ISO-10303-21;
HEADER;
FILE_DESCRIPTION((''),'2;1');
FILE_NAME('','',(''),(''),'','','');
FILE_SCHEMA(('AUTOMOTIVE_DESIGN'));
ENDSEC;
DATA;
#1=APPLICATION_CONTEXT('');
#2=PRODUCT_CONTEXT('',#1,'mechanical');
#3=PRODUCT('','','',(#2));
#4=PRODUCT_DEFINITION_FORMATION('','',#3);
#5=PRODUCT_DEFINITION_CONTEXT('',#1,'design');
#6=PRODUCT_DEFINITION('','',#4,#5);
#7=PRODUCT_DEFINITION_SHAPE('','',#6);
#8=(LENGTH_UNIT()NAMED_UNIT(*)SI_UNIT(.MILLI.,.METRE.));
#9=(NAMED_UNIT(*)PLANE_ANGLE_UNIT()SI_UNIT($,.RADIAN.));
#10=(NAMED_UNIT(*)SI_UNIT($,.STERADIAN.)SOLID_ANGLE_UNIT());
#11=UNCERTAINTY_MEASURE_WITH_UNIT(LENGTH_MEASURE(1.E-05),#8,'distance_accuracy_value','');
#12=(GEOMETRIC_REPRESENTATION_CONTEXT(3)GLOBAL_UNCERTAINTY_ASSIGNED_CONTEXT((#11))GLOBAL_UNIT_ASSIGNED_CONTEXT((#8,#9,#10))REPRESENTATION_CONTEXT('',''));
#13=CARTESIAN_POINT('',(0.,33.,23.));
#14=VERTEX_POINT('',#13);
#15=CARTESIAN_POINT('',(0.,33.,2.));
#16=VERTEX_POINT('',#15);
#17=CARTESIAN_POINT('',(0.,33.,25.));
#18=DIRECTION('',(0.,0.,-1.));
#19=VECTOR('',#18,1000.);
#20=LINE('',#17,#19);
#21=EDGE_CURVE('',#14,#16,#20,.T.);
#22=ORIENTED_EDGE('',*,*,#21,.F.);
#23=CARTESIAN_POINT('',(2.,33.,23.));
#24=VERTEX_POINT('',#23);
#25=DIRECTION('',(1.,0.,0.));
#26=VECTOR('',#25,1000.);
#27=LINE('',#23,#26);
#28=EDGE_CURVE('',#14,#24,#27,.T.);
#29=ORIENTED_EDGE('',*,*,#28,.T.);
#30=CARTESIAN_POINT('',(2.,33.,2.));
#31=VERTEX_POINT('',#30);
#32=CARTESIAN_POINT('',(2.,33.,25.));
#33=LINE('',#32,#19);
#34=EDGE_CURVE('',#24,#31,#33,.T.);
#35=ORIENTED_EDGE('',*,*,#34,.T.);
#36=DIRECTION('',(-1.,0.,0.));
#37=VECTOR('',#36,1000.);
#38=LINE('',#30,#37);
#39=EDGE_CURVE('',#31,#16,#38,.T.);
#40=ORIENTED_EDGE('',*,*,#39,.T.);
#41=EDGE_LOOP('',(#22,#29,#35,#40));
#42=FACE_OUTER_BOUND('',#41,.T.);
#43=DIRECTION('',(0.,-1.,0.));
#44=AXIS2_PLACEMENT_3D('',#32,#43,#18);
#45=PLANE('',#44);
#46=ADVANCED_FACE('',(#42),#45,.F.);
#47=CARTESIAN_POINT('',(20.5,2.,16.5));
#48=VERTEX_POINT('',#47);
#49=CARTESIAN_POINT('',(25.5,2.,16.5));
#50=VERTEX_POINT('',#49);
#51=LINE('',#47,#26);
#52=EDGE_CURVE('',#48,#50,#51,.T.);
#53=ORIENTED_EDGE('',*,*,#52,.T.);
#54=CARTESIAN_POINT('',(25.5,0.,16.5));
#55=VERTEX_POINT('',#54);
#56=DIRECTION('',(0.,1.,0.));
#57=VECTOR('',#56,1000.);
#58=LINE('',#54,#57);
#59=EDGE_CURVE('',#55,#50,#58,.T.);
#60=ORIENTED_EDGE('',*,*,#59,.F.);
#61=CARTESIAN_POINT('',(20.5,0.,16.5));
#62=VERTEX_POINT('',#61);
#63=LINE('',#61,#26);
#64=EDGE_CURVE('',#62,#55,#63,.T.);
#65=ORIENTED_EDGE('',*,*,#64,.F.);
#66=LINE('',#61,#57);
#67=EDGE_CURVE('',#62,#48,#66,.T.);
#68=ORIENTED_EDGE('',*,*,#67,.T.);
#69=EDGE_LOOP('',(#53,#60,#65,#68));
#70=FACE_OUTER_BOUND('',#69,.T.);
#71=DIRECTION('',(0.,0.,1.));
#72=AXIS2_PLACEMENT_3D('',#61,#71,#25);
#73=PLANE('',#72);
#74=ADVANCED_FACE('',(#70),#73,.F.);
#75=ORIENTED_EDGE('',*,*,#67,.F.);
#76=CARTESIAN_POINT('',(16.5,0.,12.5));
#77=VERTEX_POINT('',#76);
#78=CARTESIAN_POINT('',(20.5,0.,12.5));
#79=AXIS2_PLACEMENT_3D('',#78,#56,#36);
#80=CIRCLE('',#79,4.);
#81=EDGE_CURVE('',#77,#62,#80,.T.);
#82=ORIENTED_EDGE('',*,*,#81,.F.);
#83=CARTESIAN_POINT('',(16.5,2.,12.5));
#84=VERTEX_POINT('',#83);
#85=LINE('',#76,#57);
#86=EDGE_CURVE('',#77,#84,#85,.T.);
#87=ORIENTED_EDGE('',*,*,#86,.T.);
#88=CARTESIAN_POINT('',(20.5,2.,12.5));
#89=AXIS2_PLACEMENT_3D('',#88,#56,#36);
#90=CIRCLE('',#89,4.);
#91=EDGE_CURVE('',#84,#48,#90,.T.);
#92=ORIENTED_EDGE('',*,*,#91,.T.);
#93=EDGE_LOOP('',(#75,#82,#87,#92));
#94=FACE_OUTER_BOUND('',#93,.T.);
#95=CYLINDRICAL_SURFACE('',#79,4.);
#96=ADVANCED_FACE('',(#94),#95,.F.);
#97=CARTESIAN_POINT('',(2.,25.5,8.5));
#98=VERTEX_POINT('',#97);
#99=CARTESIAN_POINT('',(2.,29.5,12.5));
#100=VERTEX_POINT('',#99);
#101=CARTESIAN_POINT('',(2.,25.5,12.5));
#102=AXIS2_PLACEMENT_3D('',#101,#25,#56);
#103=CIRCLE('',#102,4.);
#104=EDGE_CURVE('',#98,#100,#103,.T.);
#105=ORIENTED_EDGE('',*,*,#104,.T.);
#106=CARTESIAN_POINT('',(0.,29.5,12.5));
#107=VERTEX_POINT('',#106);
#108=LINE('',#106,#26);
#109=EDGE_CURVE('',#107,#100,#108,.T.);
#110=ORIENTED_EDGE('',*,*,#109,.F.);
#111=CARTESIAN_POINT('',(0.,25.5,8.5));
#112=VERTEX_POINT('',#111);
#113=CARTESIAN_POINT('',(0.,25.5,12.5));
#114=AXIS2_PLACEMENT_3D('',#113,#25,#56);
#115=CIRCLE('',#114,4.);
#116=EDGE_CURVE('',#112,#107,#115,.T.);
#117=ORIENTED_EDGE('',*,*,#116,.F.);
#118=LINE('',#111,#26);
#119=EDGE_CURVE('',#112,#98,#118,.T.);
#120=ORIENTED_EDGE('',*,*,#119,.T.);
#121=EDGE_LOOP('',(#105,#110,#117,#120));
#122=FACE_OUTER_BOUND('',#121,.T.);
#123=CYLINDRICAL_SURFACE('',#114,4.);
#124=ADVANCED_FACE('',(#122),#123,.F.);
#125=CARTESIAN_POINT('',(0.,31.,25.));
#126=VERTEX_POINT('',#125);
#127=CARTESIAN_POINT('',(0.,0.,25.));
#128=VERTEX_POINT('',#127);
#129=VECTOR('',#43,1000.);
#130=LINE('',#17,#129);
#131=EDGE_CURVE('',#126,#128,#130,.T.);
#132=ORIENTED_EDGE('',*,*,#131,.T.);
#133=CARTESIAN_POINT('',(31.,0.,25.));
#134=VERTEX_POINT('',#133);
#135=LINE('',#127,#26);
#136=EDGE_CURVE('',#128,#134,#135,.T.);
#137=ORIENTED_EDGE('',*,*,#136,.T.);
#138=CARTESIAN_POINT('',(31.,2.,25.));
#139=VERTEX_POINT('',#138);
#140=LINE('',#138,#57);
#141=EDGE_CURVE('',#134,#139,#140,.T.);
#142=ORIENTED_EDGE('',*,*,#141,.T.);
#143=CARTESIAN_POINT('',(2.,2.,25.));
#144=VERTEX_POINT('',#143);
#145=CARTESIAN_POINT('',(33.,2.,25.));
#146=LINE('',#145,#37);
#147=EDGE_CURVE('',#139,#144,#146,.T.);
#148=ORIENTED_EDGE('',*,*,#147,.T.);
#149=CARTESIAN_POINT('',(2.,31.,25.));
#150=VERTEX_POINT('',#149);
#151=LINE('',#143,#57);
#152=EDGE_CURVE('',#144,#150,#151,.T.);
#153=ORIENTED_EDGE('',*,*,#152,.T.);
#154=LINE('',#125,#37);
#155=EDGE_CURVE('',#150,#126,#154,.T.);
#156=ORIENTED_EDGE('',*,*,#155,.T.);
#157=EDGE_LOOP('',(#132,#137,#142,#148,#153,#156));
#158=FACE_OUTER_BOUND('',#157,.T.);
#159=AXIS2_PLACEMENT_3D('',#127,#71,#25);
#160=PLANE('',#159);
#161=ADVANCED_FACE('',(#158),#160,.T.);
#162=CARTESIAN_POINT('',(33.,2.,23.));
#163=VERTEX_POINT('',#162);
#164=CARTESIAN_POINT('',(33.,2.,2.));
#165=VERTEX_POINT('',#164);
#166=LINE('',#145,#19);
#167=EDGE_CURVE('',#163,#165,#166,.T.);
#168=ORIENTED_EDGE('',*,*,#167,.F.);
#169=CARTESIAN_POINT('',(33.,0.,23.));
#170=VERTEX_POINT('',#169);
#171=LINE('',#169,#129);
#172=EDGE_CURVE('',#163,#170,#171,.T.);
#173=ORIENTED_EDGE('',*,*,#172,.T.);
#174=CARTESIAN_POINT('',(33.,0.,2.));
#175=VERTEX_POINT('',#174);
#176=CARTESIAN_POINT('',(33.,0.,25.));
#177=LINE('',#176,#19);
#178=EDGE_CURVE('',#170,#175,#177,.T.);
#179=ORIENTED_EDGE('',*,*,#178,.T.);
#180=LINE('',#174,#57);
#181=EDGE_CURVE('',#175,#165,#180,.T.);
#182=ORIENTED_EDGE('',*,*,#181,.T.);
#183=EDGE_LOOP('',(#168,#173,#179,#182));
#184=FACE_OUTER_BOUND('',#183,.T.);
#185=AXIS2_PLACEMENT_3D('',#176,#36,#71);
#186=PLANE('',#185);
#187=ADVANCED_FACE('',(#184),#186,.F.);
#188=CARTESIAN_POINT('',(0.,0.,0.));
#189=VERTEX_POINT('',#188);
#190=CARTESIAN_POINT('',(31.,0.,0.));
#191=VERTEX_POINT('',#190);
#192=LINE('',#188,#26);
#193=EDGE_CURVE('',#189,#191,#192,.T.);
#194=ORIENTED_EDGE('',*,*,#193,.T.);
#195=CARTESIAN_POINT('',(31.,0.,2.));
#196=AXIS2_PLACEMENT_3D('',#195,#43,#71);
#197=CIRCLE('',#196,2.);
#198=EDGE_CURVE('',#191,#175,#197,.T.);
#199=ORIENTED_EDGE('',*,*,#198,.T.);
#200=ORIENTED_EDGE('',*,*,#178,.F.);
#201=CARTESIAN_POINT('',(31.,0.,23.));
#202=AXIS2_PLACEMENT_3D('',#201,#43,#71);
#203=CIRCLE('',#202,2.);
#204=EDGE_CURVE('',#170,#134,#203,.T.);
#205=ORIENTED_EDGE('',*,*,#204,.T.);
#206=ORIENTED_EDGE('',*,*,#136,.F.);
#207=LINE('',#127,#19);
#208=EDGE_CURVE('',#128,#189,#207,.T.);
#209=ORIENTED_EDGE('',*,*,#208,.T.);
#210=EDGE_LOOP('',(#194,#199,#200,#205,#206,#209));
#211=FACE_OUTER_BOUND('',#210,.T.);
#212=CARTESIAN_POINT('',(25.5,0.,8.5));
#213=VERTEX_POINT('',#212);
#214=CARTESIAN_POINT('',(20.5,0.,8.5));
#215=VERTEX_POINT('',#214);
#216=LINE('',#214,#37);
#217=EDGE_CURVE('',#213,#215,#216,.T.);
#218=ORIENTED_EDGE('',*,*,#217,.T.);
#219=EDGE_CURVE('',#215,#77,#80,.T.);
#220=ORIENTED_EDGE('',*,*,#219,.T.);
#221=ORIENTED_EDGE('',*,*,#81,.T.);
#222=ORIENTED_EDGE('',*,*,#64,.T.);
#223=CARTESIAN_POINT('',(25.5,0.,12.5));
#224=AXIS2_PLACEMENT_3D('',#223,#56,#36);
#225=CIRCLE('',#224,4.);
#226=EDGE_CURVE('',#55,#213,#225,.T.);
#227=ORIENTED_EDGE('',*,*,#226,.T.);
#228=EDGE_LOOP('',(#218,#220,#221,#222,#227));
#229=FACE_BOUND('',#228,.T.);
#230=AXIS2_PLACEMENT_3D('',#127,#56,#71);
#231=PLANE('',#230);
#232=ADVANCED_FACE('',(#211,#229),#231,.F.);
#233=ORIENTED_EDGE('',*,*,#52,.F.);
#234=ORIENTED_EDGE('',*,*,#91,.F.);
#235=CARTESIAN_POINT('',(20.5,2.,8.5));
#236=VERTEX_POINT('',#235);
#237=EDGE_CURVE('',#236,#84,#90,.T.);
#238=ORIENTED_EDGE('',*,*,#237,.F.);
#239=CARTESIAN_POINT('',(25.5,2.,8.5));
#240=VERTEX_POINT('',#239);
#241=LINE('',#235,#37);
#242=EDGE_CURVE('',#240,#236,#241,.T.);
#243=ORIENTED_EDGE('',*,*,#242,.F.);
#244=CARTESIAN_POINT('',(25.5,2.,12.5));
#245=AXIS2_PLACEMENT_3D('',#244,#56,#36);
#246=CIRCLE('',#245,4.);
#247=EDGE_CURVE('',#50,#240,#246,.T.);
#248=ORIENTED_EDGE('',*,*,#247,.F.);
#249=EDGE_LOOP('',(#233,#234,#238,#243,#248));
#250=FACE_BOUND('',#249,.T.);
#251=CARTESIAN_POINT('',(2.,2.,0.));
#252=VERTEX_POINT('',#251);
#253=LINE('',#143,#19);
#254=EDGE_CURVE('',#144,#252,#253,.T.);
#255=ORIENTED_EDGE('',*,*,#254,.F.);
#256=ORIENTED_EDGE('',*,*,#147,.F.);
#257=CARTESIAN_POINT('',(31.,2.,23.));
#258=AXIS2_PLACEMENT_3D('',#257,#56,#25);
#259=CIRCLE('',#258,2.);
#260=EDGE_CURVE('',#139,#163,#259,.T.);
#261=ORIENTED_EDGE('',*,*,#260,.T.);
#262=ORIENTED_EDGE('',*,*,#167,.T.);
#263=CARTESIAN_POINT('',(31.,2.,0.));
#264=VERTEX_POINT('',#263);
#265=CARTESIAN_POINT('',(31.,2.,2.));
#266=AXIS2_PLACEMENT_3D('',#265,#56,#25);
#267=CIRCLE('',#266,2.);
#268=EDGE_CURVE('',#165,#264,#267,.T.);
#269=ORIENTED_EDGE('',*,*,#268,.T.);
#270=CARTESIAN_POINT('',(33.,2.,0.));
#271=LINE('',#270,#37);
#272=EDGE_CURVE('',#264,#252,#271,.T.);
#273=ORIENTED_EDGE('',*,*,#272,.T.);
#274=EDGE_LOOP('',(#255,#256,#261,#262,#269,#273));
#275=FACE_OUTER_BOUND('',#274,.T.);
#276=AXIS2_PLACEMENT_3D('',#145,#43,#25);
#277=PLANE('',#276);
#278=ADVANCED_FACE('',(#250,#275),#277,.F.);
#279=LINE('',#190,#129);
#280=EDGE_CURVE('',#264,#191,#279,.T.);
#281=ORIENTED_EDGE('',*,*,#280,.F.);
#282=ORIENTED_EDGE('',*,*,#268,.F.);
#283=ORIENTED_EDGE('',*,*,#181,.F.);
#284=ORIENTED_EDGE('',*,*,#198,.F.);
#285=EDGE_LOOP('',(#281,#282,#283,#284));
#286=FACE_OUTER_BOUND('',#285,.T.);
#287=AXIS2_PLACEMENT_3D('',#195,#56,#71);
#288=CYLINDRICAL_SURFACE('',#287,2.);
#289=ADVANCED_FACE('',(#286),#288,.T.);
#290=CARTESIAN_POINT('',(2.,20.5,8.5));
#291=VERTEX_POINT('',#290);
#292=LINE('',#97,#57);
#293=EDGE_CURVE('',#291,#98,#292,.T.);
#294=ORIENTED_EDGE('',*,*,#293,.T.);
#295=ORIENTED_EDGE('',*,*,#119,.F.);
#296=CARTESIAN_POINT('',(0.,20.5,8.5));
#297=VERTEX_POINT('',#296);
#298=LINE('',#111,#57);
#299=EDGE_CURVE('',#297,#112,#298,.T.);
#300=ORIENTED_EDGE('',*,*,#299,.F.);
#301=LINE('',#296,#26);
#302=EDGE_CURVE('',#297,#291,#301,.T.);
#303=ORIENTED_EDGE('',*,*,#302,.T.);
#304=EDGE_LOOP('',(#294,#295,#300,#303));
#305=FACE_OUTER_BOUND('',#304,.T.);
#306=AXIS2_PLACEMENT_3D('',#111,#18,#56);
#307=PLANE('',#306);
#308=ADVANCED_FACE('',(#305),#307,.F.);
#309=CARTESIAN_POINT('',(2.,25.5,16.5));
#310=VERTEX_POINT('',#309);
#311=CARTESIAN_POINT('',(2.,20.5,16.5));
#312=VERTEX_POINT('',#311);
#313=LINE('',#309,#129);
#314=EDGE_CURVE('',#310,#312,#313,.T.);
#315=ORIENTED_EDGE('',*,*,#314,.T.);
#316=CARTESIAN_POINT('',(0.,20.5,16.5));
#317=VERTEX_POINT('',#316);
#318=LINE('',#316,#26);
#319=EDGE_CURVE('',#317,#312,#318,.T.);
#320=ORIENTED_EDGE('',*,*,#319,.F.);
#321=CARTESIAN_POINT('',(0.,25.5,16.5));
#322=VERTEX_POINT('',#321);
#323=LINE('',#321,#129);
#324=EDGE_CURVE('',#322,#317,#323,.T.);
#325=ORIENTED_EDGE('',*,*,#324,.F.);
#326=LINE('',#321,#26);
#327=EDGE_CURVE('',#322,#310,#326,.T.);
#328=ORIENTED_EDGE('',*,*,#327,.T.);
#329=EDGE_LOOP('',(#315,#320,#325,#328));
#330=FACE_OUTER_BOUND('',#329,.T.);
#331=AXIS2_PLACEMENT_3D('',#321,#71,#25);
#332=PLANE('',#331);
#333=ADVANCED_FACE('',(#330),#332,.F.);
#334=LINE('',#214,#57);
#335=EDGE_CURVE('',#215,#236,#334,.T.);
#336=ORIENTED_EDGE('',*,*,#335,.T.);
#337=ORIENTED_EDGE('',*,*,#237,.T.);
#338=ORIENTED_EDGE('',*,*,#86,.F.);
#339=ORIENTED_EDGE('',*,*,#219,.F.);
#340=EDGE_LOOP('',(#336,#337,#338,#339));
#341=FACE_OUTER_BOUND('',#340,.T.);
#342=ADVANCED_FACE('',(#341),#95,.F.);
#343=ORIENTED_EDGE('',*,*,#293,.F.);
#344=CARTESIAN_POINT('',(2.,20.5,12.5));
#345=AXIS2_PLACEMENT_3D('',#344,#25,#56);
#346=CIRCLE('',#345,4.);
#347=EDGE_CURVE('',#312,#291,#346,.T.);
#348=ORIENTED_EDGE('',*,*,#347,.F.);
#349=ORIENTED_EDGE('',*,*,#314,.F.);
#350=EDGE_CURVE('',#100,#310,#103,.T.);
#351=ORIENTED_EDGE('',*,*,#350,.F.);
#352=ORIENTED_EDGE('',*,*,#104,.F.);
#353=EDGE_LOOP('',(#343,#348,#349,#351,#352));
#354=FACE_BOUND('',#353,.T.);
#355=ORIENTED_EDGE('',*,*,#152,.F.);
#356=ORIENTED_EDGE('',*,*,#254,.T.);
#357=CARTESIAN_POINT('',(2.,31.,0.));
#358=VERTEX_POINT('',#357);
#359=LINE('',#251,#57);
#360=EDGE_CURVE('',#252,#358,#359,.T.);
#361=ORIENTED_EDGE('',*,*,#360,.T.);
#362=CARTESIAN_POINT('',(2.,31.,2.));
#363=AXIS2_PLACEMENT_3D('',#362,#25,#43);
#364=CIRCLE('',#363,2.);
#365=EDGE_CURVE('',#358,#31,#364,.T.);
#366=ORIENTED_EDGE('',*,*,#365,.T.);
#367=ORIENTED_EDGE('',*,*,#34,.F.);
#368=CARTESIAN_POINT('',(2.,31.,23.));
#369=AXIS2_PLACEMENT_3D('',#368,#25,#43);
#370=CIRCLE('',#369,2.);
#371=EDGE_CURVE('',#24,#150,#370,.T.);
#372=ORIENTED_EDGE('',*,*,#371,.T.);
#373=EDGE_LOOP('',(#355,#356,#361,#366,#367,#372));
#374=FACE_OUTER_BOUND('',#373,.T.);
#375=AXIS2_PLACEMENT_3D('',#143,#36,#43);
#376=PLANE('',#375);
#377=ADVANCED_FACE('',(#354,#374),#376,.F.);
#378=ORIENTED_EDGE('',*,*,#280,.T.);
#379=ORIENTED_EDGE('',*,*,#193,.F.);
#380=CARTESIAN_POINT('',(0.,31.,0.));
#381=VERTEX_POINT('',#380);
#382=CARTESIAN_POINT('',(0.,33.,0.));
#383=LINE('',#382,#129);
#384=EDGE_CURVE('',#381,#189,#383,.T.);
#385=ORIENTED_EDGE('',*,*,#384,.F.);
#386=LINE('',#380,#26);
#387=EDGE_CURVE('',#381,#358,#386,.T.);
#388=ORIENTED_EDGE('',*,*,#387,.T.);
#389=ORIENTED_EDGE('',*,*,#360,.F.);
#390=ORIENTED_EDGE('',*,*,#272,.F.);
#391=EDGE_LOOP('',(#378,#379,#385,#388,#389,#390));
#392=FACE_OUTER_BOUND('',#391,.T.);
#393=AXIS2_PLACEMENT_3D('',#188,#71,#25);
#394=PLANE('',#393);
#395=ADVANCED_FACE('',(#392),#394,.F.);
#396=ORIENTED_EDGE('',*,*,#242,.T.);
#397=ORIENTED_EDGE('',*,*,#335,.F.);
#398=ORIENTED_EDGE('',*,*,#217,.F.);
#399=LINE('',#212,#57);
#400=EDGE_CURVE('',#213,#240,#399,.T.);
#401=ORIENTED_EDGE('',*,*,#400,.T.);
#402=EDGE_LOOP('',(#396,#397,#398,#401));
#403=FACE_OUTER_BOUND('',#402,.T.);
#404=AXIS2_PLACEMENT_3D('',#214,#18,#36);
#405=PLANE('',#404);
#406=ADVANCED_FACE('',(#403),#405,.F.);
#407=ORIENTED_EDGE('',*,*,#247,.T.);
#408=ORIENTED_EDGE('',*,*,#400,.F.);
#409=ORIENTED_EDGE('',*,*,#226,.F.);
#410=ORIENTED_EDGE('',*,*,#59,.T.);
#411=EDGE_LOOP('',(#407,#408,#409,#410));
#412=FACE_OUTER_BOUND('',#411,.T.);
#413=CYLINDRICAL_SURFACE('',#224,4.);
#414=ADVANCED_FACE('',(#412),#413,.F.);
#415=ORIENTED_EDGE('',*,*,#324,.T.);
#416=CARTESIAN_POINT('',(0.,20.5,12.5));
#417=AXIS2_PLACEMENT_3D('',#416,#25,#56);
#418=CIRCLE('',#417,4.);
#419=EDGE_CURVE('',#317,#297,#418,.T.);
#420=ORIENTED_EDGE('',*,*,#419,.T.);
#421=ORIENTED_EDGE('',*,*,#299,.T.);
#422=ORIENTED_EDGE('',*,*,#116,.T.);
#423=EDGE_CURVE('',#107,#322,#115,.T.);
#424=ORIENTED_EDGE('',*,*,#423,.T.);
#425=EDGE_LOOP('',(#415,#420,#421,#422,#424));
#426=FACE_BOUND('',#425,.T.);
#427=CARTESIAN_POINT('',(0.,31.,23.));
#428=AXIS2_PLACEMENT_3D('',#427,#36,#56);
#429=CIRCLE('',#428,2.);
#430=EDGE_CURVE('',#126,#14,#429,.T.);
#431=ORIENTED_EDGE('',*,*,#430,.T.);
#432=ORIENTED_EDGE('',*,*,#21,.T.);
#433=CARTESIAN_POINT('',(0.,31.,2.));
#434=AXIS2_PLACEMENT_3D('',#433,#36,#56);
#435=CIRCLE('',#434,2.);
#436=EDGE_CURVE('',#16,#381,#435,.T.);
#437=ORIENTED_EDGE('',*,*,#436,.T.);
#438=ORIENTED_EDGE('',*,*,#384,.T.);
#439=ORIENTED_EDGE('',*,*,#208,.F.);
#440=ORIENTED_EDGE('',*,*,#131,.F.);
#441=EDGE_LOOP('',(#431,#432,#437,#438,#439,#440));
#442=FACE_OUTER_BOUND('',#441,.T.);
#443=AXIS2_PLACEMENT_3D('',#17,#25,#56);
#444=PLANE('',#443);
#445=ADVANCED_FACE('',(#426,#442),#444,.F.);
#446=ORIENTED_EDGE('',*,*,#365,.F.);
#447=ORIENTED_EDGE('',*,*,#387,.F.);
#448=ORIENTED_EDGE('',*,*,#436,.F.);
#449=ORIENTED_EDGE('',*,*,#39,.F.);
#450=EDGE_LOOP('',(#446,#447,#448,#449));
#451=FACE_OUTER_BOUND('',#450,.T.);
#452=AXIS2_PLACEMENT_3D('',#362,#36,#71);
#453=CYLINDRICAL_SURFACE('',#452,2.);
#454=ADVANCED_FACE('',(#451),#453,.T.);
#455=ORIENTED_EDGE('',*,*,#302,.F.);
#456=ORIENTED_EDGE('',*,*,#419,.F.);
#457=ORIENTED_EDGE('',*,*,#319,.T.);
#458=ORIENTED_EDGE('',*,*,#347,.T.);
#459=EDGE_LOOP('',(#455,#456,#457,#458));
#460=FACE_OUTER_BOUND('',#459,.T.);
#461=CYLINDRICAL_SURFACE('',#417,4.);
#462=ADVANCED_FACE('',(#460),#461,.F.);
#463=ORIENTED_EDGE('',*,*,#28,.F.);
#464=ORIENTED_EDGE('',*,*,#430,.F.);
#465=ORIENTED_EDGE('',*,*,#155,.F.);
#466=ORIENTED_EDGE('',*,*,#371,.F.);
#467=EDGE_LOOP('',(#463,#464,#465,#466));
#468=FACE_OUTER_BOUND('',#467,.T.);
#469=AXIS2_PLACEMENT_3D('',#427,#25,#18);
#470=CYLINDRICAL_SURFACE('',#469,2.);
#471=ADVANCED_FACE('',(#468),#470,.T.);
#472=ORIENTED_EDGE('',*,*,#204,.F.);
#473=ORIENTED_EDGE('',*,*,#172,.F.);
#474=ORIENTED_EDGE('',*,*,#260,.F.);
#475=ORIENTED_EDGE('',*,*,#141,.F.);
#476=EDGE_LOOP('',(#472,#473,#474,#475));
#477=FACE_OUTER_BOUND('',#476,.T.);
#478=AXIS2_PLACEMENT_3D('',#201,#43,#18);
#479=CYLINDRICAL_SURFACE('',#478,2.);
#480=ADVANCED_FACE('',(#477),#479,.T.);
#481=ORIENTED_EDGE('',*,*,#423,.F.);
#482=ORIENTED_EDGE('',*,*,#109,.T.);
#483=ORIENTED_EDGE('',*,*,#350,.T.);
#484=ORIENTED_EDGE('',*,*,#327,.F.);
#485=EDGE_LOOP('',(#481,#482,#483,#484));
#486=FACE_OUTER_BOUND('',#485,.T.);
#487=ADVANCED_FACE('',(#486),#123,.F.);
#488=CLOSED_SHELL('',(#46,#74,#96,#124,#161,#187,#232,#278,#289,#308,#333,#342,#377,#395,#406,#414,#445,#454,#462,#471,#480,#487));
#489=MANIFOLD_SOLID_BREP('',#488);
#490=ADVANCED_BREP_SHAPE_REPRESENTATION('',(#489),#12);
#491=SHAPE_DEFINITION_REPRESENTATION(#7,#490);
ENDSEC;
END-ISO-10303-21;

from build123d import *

# Parameters (mm, degrees)
EXTRUDE_1_DEPTH     = 25
FILLET_1_R          = 2
CUT_EXTRUDE_1_DEPTH = 52.720402164
CUT_EXTRUDE_2_DEPTH = 52.720402164


with BuildPart() as part:
    # 草图1 → 凸台-拉伸1 (new body)
    with BuildSketch(Plane.XY):
        Polygon((0, 0), (33, 0), (33, 2), (2, 2), (2, 33), (0, 33), align=None)
    extrude(amount=EXTRUDE_1_DEPTH)

    # 圆角1
    fillet_1_edges = [part.edges().sort_by_distance(p)[0] for p in [
        (33, 1, 25),
        (1, 33, 25),
        (1, 33, 0),
        (33, 1, 0),
    ]]
    fillet(fillet_1_edges, radius=FILLET_1_R)

    # 草图2 → 切除-拉伸1 (cut, through all)
    with BuildSketch(Plane(origin=(0, 2, 0), x_dir=(1, 0, 0), z_dir=(0, 1, 0))):
        with BuildLine():
            Line((20.5, -8.5), (25.5, -8.5))
            ThreePointArc((25.5, -8.5), (29.5, -12.5), (25.5, -16.5))
            Line((25.5, -16.5), (20.5, -16.5))
            ThreePointArc((20.5, -16.5), (16.5, -12.5), (20.5, -8.5))
        make_face()
    extrude(amount=-CUT_EXTRUDE_1_DEPTH, mode=Mode.SUBTRACT)

    # 草图4 → 切除-拉伸2 (cut, through all)
    with BuildSketch(Plane(origin=(2, 0, 0), x_dir=(0, 0, -1), z_dir=(1, 0, 0))):
        with BuildLine():
            Line((-8.5, 25.5), (-8.5, 20.5))
            ThreePointArc((-8.5, 20.5), (-12.5, 16.5), (-16.5, 20.5))
            Line((-16.5, 20.5), (-16.5, 25.5))
            ThreePointArc((-16.5, 25.5), (-12.5, 29.5), (-8.5, 25.5))
        make_face()
    extrude(amount=-CUT_EXTRUDE_2_DEPTH, mode=Mode.SUBTRACT)


solid = part.part
